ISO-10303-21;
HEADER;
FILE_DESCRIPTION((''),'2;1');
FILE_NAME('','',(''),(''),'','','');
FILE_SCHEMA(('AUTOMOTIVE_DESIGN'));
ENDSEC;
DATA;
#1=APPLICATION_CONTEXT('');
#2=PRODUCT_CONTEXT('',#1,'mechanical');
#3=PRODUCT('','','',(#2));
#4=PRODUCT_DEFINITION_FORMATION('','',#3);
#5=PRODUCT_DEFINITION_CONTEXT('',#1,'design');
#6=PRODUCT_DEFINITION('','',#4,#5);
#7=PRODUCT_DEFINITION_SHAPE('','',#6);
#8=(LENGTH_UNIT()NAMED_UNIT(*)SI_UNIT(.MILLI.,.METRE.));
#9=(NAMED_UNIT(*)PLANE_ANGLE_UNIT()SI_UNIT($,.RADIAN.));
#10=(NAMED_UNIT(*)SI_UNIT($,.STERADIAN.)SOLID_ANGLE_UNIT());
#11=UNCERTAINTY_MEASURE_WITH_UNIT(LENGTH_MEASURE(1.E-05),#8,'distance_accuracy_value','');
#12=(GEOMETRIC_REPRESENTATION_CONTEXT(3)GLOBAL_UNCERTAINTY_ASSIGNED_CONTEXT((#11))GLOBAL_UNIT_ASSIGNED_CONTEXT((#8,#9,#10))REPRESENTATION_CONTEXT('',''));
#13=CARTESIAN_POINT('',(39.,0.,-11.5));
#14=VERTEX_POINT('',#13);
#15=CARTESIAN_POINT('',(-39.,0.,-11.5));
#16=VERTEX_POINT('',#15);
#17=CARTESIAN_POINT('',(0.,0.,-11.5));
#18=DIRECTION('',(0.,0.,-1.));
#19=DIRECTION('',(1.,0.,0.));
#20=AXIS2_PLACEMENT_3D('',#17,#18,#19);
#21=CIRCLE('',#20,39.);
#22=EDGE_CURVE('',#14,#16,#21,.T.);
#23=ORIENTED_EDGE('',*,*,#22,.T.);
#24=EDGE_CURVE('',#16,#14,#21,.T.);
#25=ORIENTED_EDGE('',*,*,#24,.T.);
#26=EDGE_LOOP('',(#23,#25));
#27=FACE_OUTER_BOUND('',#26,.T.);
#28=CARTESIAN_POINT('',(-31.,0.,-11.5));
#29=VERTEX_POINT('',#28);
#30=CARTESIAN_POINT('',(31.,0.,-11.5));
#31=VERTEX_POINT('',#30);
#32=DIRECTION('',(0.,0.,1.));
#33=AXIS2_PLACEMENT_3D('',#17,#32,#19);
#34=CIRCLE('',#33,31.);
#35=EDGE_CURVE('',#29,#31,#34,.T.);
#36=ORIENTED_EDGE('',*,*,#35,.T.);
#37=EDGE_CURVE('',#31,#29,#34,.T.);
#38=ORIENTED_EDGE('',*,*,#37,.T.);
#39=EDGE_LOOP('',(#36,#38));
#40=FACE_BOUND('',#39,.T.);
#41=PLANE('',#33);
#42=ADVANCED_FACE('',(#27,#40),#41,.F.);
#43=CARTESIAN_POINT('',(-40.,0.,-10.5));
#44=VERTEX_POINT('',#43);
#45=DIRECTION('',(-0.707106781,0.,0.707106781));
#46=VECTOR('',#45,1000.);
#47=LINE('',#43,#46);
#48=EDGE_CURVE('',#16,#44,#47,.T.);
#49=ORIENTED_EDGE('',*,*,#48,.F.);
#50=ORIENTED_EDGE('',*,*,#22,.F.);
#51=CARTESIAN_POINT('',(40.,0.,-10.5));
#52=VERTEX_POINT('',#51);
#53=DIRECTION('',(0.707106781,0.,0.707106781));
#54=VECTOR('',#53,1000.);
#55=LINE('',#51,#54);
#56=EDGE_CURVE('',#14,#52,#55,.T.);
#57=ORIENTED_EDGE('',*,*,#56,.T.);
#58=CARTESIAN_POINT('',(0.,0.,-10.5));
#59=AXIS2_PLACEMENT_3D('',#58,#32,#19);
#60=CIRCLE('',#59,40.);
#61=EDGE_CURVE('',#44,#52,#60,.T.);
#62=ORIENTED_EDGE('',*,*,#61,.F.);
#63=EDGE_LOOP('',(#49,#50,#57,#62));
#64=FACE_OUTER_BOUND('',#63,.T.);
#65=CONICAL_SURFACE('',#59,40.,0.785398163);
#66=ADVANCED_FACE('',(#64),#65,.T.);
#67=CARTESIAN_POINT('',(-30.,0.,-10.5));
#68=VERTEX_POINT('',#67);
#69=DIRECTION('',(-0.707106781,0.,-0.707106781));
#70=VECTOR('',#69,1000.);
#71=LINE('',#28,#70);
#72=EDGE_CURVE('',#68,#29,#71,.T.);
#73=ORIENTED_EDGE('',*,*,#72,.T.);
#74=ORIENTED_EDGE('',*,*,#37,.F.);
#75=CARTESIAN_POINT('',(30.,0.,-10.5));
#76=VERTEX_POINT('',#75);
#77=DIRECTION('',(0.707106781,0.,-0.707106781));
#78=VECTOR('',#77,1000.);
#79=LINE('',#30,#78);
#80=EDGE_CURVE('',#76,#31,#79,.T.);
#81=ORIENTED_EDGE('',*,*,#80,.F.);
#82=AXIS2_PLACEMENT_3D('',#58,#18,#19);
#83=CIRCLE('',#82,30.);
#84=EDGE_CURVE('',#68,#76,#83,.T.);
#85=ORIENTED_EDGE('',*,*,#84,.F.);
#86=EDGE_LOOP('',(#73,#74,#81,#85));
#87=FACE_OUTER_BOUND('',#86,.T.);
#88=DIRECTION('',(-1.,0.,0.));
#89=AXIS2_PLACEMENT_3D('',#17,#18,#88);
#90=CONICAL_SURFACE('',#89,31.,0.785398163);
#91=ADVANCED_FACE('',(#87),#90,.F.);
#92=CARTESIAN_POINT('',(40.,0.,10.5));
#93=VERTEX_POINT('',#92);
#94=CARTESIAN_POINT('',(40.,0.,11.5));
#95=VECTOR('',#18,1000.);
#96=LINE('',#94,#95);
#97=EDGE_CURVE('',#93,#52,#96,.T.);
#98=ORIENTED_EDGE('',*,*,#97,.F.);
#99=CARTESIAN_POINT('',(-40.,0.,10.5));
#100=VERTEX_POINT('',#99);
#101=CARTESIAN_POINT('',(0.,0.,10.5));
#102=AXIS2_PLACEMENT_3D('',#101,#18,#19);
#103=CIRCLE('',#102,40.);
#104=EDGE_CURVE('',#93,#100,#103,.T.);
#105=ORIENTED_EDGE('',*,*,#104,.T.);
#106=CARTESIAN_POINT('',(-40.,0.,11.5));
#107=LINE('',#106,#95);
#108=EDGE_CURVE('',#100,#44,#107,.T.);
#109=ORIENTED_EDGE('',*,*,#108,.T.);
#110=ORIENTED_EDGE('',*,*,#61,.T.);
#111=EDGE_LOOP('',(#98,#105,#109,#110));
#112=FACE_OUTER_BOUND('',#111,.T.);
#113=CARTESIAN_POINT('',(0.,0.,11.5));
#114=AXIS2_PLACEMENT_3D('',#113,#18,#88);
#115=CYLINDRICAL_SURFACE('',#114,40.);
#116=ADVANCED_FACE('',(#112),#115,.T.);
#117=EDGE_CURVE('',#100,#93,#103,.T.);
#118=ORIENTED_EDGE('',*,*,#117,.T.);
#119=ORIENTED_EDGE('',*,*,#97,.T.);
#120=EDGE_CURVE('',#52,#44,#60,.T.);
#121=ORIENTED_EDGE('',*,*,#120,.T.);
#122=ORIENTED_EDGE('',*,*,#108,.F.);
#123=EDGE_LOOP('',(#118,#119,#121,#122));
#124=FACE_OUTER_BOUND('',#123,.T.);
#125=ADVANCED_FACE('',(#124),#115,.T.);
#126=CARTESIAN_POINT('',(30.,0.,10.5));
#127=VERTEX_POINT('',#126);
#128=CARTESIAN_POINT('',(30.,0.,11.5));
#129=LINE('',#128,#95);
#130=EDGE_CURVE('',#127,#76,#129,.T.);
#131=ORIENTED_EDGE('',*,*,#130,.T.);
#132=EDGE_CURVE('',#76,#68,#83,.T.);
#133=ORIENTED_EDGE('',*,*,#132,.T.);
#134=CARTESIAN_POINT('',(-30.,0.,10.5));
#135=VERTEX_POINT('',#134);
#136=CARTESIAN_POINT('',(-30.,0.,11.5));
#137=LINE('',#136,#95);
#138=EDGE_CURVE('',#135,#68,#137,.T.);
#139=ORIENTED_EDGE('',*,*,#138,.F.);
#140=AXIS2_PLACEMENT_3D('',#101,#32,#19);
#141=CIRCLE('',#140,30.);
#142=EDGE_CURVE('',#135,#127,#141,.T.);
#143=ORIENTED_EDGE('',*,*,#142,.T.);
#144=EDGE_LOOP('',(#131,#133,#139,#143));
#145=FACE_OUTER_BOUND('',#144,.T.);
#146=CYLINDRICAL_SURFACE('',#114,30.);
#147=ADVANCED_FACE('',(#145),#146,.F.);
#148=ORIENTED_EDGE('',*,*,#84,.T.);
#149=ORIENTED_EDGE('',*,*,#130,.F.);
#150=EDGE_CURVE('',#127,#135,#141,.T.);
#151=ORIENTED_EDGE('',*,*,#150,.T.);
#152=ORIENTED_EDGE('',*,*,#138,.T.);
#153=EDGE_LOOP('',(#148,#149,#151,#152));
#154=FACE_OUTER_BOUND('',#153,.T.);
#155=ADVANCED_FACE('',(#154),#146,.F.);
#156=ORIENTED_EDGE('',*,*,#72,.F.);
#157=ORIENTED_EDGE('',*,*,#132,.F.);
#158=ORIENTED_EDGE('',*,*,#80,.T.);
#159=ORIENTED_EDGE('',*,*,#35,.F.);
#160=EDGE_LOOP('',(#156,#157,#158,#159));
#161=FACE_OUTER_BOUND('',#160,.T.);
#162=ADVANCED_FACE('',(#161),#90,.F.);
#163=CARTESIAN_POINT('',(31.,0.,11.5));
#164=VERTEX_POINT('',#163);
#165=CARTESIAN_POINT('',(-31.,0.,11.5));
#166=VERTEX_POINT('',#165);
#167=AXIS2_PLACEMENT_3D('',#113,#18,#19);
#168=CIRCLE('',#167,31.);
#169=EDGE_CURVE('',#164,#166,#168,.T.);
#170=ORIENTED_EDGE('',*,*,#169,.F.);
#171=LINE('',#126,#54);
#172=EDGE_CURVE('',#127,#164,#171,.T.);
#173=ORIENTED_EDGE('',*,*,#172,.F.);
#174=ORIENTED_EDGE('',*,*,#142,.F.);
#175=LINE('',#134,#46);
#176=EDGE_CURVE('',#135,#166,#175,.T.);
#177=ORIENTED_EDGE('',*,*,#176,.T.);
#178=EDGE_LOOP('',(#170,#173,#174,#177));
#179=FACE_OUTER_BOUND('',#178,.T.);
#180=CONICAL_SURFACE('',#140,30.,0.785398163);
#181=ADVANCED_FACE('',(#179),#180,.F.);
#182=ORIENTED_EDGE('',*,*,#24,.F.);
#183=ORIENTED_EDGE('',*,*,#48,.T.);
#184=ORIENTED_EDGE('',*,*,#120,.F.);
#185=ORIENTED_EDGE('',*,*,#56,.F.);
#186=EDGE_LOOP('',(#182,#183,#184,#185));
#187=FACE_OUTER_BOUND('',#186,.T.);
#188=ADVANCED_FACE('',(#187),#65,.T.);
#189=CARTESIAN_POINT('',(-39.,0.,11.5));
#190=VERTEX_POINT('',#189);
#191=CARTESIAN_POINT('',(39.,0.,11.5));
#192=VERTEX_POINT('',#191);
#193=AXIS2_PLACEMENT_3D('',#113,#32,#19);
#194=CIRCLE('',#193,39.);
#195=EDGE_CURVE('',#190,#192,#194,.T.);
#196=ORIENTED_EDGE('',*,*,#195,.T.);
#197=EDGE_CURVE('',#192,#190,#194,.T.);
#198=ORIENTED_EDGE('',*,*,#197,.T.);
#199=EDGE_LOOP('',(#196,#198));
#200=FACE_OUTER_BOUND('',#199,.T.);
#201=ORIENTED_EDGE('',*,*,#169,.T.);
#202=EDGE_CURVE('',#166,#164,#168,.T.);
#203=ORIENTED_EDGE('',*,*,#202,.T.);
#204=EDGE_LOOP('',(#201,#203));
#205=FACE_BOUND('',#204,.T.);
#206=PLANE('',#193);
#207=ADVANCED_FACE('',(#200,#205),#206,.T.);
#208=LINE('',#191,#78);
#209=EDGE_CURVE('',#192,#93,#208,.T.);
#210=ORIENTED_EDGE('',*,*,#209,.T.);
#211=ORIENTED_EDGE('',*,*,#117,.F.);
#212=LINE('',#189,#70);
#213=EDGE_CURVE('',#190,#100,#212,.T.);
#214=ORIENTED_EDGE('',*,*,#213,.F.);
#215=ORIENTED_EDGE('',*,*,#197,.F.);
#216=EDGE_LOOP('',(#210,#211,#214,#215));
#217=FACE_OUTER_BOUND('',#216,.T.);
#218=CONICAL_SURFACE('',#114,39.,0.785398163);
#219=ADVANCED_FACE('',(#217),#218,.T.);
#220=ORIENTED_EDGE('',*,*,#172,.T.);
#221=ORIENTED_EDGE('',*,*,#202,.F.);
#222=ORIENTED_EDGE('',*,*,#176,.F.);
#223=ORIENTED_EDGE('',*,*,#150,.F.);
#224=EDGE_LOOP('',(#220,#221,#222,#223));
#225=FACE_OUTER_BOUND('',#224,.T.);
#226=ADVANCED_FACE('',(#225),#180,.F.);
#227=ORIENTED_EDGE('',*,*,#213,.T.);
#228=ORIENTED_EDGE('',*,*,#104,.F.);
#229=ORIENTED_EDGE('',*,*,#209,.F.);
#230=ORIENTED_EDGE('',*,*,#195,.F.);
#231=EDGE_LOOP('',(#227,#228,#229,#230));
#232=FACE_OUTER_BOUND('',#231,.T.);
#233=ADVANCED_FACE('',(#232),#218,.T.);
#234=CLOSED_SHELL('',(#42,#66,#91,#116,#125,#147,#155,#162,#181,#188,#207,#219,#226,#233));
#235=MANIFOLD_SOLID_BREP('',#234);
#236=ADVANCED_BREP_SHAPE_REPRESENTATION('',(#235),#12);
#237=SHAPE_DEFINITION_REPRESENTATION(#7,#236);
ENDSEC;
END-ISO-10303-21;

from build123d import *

# Parameters (mm, degrees)
SKETCH1_R           = 40
SKETCH1_R_2         = 30
BOSS_EXTRUDE1_DEPTH = 11.5
CHAMFER1_SIZE       = 1


with BuildPart() as part:
    # Sketch1 → Boss-Extrude1 (new, symmetric)
    with BuildSketch(Plane.XY):
        Circle(SKETCH1_R)
        Circle(SKETCH1_R_2, mode=Mode.SUBTRACT)
    extrude(amount=BOSS_EXTRUDE1_DEPTH, both=True)

    # Chamfer1
    chamfer1_edges = [part.edges().sort_by_distance(p)[0] for p in [
        (-40, 0, -11.5),
        (-40, 0, 11.5),
        (-30, 0, -11.5),
        (-30, 0, 11.5),
    ]]
    chamfer(chamfer1_edges, length=CHAMFER1_SIZE)


solid = part.part
